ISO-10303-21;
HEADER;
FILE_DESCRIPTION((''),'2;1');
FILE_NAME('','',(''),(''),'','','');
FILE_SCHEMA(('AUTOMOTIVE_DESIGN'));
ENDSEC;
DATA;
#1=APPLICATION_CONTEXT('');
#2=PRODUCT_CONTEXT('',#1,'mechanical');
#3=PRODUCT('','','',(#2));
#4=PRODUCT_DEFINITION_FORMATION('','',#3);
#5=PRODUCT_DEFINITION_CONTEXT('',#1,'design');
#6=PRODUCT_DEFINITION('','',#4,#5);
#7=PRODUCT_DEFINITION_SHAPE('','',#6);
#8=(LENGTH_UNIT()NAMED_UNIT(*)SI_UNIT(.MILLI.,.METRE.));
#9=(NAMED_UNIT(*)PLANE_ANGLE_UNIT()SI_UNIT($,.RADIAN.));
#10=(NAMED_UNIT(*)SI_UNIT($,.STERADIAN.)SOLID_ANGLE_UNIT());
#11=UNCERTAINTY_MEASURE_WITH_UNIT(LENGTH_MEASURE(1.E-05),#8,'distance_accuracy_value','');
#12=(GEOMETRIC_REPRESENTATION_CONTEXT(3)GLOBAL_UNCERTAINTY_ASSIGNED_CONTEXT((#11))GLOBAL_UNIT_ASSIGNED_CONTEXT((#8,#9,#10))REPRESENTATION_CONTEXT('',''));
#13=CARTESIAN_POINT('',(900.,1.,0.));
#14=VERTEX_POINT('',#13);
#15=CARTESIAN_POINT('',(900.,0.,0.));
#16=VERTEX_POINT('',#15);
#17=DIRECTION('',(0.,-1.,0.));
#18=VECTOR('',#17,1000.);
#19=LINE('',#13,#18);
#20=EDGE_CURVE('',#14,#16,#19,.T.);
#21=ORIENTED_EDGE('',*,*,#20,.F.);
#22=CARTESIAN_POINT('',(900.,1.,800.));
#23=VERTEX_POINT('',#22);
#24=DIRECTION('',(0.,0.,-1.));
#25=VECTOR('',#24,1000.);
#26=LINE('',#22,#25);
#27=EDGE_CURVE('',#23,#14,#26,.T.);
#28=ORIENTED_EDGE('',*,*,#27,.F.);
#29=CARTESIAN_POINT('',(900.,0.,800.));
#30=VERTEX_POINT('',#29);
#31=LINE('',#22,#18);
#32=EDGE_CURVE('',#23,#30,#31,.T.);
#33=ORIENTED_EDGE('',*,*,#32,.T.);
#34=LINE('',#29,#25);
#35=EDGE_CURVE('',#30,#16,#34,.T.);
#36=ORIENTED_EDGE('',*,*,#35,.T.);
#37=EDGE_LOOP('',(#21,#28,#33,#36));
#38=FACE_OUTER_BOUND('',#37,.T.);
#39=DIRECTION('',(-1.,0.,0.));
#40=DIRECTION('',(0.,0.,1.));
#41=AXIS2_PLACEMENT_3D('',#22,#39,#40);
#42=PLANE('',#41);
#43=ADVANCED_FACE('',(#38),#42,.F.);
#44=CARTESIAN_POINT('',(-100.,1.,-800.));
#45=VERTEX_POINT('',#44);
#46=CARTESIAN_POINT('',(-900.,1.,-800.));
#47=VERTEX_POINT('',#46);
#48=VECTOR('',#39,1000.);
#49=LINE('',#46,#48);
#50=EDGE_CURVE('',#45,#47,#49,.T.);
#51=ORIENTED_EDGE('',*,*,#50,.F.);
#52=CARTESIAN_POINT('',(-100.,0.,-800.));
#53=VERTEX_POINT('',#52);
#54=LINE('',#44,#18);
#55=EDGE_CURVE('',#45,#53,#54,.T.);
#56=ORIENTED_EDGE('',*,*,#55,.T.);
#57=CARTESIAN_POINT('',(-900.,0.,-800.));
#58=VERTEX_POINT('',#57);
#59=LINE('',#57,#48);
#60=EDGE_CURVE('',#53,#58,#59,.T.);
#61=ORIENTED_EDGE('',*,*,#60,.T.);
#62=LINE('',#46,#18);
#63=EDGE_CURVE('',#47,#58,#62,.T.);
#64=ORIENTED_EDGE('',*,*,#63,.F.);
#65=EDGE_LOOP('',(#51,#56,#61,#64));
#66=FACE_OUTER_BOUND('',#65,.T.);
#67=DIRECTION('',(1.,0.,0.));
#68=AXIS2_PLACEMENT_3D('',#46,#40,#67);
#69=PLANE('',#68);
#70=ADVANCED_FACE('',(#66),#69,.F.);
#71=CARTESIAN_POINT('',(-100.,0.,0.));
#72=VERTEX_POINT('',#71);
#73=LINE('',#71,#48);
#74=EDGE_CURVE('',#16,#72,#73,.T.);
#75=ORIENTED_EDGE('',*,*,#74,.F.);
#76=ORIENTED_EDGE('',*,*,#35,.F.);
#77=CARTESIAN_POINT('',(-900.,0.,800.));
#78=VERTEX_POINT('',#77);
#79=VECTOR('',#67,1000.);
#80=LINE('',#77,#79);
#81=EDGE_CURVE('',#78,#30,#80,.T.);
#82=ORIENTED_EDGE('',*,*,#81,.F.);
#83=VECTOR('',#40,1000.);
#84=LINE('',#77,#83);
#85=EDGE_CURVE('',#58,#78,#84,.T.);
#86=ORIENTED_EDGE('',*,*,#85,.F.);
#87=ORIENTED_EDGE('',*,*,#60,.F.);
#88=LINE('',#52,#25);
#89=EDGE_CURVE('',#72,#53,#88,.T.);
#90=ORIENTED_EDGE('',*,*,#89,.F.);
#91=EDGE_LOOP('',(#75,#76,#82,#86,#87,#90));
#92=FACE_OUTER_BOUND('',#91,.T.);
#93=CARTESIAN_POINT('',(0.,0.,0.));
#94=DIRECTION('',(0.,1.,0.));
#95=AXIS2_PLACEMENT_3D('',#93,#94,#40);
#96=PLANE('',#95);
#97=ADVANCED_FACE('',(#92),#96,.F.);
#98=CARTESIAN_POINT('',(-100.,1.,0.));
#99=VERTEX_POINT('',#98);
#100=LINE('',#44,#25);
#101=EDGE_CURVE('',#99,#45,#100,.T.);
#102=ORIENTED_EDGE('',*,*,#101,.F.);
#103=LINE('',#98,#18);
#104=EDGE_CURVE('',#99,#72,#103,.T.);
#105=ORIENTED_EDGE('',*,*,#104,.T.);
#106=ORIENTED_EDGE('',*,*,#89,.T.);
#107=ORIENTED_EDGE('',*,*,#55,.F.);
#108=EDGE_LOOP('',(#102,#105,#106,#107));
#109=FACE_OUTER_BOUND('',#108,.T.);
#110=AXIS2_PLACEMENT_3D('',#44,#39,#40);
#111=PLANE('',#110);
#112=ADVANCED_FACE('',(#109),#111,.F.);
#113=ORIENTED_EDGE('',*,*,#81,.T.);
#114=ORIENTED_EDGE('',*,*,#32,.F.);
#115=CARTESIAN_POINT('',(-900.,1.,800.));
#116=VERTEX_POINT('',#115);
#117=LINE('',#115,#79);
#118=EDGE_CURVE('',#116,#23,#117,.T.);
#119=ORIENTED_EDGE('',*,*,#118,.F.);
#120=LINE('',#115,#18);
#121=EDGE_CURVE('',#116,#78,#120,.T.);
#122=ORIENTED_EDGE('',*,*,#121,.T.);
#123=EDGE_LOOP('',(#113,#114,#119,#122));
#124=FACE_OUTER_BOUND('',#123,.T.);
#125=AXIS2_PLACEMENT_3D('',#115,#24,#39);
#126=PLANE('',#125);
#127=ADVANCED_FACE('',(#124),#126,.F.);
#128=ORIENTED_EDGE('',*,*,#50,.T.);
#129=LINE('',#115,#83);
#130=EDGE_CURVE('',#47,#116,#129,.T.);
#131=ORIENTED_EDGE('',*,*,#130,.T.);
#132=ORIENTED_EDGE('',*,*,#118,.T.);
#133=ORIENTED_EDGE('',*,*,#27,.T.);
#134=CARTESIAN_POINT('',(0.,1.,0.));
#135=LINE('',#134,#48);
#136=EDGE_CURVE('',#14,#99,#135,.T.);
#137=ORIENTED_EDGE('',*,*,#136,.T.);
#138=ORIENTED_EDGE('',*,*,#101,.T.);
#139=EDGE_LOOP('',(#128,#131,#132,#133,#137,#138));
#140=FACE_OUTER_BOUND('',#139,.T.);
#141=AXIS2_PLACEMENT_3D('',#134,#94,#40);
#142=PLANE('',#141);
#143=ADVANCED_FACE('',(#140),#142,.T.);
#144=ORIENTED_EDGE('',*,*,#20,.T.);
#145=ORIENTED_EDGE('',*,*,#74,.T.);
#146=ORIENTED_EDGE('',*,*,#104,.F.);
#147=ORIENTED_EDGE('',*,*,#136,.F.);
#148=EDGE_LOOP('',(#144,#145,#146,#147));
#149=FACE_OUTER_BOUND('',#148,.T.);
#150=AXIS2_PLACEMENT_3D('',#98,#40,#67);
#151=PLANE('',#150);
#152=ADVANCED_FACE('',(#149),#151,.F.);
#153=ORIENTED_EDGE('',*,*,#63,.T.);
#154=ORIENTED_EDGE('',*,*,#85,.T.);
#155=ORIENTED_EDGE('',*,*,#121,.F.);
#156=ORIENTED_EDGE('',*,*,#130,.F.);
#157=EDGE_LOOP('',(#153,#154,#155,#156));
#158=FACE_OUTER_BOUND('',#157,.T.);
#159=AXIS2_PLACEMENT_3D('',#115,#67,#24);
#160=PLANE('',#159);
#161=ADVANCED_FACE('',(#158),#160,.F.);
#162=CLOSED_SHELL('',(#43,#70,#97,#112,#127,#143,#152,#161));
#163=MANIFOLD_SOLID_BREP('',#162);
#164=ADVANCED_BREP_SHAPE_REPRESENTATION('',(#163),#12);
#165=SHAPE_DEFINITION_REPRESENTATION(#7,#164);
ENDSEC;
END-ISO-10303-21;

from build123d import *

# Parameters (mm, degrees)
BOSS_EXTRUDE1_DEPTH = 1


with BuildPart() as part:
    # Sketch1 → Boss-Extrude1 (new body)
    with BuildSketch(Plane(origin=(0, 0, 0), x_dir=(1, 0, 0), z_dir=(0, 1, 0))):
        Polygon((-900, -800), (900, -800), (900, 0), (0, 0), (-100, 0), (-100, 800), (-900, 800), align=None)
    extrude(amount=BOSS_EXTRUDE1_DEPTH)


solid = part.part
